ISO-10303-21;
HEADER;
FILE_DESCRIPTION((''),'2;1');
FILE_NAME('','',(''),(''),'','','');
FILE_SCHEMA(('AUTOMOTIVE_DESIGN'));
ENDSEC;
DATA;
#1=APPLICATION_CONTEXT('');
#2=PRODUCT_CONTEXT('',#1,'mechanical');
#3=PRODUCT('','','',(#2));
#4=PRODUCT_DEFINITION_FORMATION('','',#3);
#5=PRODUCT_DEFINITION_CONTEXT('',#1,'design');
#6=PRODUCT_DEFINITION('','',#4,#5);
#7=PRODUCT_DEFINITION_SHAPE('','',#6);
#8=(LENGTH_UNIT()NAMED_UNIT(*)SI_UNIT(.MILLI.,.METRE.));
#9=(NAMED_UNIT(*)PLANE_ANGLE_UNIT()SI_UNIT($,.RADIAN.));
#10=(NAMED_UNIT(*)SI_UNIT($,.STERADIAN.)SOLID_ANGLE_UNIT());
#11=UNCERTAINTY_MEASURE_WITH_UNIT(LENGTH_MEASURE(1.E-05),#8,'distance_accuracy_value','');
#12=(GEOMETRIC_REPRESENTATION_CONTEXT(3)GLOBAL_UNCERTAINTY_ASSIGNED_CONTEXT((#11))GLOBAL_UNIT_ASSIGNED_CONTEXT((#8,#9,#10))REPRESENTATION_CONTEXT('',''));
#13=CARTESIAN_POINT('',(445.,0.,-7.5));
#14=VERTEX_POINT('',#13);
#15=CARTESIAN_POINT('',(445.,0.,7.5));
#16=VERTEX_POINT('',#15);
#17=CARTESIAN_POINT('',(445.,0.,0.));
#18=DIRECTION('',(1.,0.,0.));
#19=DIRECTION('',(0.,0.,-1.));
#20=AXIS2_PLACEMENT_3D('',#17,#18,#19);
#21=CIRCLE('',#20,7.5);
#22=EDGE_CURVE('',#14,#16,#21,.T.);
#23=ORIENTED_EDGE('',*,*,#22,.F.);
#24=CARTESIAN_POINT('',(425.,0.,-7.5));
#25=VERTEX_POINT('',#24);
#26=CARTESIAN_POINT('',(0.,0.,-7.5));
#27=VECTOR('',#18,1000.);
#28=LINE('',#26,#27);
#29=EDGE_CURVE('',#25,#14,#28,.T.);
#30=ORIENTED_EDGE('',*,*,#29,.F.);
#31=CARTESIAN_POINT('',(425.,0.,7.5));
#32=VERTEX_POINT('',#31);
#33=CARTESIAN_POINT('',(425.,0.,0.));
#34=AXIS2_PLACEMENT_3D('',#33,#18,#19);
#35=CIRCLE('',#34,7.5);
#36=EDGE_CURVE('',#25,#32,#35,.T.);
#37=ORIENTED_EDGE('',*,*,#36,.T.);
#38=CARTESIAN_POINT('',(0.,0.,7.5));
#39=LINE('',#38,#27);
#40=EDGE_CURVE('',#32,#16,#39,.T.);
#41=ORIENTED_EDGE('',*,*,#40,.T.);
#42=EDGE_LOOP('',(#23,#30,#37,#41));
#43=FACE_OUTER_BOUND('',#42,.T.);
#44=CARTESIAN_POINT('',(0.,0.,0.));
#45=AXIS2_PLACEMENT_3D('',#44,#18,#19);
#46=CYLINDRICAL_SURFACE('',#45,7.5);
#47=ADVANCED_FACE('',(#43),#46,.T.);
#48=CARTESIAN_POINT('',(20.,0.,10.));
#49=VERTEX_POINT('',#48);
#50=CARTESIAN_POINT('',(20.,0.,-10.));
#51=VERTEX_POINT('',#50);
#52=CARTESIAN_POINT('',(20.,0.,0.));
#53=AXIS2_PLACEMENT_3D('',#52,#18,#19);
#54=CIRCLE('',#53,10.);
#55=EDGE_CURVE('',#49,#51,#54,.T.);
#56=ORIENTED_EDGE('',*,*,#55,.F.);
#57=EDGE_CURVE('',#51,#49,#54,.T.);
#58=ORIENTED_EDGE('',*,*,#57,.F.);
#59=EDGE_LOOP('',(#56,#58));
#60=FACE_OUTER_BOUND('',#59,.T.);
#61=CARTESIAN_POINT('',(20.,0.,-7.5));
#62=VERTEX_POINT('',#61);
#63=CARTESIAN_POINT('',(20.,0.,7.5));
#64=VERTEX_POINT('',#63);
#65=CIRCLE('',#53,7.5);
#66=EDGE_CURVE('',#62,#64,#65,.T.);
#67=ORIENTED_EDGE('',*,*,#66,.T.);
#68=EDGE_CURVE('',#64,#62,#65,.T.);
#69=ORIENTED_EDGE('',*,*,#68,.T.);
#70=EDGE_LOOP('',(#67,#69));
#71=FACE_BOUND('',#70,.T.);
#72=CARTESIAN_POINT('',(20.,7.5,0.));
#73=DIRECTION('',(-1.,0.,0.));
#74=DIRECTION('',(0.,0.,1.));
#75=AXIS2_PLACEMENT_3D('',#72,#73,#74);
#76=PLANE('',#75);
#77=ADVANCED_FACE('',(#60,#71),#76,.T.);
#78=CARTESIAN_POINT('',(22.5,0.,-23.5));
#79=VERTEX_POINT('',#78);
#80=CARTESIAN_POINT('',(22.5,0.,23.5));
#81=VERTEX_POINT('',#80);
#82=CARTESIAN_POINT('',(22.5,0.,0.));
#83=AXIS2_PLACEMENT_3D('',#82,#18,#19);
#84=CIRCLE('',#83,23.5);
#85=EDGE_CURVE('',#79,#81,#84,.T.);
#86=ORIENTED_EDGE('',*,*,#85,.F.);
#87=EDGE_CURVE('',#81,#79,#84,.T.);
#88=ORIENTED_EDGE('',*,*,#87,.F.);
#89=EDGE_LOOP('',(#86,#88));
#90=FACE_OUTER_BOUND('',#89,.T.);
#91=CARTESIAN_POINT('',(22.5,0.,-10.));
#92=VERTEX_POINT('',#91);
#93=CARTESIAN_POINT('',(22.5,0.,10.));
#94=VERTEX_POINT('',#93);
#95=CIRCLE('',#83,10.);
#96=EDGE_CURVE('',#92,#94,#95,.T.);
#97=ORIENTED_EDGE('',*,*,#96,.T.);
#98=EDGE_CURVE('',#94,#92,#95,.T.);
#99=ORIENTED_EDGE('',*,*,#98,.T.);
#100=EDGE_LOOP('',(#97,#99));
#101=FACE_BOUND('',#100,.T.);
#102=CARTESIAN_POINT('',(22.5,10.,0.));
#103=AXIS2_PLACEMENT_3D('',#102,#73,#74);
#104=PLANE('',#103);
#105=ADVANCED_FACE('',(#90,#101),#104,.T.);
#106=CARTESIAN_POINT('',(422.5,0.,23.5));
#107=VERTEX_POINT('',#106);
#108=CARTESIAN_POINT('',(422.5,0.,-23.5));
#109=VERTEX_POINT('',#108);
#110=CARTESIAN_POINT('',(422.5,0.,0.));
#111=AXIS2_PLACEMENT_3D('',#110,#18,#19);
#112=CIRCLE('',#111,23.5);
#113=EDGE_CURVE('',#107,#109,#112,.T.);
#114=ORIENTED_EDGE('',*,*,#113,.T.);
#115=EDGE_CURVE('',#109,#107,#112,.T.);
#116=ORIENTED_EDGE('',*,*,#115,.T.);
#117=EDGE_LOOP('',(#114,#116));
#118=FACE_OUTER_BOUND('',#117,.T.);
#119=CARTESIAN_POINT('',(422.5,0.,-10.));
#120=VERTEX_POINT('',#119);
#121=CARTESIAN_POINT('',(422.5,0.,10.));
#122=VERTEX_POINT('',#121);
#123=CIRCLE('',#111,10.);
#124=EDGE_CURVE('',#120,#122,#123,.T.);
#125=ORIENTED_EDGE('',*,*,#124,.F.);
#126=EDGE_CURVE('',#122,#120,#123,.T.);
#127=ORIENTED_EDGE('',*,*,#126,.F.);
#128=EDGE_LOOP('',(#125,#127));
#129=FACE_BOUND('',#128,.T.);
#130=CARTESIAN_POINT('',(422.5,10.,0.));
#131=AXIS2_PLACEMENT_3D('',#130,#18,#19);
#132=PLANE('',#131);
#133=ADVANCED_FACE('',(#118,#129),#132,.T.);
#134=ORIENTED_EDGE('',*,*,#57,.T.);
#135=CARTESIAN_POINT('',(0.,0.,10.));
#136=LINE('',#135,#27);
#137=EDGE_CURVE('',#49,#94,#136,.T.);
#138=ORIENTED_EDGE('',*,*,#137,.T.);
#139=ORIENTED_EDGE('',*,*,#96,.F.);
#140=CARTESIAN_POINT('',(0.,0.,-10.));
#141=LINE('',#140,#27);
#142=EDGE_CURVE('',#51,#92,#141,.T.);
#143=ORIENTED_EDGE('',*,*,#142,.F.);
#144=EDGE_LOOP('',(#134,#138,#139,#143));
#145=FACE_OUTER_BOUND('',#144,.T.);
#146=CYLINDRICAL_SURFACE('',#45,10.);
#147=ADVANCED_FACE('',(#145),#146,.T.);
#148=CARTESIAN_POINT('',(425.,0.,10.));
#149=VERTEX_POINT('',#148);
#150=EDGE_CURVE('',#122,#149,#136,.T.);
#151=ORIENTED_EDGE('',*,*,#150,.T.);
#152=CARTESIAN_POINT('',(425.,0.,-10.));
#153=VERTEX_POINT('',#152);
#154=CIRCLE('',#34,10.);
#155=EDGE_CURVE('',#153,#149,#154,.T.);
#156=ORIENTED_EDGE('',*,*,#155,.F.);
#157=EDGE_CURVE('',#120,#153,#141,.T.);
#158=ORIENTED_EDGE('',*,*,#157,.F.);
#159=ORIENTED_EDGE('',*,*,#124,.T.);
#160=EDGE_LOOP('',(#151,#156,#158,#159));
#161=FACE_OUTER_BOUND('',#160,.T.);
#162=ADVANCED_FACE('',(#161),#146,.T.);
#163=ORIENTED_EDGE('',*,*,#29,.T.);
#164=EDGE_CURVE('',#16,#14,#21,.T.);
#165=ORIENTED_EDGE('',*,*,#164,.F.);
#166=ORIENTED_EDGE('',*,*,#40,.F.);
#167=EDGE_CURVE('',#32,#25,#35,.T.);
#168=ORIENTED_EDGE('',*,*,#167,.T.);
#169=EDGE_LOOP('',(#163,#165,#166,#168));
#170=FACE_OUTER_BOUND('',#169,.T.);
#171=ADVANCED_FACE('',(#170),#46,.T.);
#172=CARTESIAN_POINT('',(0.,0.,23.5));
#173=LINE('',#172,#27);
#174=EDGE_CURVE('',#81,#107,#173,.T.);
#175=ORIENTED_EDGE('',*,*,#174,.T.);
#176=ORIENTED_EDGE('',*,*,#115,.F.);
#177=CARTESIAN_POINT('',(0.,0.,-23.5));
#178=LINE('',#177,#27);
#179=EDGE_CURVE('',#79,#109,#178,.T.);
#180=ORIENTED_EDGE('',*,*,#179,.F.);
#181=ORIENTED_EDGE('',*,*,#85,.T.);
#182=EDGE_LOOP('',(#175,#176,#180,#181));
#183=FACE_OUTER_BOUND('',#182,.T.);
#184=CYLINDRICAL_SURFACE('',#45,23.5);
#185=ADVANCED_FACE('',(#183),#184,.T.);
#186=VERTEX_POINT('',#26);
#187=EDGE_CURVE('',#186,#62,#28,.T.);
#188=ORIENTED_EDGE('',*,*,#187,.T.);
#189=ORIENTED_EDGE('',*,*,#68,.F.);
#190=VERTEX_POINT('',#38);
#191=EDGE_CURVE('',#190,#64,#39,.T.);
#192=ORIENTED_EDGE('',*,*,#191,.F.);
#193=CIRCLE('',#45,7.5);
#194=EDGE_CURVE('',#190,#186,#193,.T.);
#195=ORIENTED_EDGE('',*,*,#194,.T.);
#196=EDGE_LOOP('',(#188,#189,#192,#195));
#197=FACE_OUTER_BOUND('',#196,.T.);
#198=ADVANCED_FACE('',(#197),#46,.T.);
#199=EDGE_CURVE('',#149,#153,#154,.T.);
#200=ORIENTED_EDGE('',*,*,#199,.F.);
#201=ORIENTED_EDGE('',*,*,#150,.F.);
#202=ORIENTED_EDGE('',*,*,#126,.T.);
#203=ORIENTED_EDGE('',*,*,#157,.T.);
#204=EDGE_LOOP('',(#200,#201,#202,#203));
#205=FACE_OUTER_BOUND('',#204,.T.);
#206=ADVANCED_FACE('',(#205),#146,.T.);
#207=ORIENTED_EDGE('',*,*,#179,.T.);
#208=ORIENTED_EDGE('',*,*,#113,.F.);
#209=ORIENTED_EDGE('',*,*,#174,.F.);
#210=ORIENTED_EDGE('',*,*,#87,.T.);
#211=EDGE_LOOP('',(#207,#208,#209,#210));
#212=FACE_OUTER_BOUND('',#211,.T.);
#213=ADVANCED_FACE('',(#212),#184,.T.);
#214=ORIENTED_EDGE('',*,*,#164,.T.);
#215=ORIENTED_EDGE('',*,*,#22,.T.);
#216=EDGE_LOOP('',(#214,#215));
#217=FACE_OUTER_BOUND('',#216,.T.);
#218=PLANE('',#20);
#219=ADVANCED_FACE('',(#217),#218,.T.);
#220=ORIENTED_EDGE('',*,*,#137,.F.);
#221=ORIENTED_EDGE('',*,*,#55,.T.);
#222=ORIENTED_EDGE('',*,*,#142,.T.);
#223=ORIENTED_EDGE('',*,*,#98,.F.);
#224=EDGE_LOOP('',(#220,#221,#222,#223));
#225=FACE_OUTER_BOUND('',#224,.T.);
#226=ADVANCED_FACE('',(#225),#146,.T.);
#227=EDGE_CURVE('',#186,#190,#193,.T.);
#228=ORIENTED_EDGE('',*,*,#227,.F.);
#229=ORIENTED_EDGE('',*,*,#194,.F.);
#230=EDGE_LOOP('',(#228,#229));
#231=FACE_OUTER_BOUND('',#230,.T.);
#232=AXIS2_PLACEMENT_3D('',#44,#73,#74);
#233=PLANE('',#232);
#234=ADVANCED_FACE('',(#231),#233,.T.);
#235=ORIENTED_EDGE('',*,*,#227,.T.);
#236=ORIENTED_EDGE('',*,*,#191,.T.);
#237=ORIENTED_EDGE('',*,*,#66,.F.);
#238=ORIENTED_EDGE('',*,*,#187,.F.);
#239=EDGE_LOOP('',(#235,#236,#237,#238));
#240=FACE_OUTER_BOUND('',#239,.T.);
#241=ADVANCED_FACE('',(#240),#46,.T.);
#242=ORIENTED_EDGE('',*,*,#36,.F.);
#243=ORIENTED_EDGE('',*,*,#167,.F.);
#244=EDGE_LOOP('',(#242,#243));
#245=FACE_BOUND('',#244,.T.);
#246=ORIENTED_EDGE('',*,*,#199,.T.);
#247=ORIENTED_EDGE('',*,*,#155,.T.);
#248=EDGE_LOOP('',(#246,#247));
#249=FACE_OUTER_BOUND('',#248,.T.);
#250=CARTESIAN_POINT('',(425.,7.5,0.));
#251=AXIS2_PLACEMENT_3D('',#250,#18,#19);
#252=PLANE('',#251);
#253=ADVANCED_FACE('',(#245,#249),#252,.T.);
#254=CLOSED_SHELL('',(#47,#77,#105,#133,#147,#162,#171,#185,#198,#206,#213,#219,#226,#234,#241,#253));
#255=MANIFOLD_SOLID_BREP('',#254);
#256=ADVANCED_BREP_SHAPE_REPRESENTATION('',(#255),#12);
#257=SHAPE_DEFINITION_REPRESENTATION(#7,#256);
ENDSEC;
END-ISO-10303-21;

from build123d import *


with BuildPart() as part:
    # Sketch1 → Revolve1 (revolve)
    with BuildSketch(Plane.XY, mode=Mode.PRIVATE) as revolve1_sk:
        Polygon((0, 0), (0, 7.5), (20, 7.5), (20, 10), (22.5, 10), (22.5, 23.5), (422.5, 23.5), (422.5, 10), (425, 10), (425, 7.5), (445, 7.5), (445, 0), align=None)
    revolve(revolve1_sk.sketch.rotate(Axis((0, 0, 0), (-1, 0, 0)), 90), axis=Axis((0, 0, 0), (-1, 0, 0)))


solid = part.part
